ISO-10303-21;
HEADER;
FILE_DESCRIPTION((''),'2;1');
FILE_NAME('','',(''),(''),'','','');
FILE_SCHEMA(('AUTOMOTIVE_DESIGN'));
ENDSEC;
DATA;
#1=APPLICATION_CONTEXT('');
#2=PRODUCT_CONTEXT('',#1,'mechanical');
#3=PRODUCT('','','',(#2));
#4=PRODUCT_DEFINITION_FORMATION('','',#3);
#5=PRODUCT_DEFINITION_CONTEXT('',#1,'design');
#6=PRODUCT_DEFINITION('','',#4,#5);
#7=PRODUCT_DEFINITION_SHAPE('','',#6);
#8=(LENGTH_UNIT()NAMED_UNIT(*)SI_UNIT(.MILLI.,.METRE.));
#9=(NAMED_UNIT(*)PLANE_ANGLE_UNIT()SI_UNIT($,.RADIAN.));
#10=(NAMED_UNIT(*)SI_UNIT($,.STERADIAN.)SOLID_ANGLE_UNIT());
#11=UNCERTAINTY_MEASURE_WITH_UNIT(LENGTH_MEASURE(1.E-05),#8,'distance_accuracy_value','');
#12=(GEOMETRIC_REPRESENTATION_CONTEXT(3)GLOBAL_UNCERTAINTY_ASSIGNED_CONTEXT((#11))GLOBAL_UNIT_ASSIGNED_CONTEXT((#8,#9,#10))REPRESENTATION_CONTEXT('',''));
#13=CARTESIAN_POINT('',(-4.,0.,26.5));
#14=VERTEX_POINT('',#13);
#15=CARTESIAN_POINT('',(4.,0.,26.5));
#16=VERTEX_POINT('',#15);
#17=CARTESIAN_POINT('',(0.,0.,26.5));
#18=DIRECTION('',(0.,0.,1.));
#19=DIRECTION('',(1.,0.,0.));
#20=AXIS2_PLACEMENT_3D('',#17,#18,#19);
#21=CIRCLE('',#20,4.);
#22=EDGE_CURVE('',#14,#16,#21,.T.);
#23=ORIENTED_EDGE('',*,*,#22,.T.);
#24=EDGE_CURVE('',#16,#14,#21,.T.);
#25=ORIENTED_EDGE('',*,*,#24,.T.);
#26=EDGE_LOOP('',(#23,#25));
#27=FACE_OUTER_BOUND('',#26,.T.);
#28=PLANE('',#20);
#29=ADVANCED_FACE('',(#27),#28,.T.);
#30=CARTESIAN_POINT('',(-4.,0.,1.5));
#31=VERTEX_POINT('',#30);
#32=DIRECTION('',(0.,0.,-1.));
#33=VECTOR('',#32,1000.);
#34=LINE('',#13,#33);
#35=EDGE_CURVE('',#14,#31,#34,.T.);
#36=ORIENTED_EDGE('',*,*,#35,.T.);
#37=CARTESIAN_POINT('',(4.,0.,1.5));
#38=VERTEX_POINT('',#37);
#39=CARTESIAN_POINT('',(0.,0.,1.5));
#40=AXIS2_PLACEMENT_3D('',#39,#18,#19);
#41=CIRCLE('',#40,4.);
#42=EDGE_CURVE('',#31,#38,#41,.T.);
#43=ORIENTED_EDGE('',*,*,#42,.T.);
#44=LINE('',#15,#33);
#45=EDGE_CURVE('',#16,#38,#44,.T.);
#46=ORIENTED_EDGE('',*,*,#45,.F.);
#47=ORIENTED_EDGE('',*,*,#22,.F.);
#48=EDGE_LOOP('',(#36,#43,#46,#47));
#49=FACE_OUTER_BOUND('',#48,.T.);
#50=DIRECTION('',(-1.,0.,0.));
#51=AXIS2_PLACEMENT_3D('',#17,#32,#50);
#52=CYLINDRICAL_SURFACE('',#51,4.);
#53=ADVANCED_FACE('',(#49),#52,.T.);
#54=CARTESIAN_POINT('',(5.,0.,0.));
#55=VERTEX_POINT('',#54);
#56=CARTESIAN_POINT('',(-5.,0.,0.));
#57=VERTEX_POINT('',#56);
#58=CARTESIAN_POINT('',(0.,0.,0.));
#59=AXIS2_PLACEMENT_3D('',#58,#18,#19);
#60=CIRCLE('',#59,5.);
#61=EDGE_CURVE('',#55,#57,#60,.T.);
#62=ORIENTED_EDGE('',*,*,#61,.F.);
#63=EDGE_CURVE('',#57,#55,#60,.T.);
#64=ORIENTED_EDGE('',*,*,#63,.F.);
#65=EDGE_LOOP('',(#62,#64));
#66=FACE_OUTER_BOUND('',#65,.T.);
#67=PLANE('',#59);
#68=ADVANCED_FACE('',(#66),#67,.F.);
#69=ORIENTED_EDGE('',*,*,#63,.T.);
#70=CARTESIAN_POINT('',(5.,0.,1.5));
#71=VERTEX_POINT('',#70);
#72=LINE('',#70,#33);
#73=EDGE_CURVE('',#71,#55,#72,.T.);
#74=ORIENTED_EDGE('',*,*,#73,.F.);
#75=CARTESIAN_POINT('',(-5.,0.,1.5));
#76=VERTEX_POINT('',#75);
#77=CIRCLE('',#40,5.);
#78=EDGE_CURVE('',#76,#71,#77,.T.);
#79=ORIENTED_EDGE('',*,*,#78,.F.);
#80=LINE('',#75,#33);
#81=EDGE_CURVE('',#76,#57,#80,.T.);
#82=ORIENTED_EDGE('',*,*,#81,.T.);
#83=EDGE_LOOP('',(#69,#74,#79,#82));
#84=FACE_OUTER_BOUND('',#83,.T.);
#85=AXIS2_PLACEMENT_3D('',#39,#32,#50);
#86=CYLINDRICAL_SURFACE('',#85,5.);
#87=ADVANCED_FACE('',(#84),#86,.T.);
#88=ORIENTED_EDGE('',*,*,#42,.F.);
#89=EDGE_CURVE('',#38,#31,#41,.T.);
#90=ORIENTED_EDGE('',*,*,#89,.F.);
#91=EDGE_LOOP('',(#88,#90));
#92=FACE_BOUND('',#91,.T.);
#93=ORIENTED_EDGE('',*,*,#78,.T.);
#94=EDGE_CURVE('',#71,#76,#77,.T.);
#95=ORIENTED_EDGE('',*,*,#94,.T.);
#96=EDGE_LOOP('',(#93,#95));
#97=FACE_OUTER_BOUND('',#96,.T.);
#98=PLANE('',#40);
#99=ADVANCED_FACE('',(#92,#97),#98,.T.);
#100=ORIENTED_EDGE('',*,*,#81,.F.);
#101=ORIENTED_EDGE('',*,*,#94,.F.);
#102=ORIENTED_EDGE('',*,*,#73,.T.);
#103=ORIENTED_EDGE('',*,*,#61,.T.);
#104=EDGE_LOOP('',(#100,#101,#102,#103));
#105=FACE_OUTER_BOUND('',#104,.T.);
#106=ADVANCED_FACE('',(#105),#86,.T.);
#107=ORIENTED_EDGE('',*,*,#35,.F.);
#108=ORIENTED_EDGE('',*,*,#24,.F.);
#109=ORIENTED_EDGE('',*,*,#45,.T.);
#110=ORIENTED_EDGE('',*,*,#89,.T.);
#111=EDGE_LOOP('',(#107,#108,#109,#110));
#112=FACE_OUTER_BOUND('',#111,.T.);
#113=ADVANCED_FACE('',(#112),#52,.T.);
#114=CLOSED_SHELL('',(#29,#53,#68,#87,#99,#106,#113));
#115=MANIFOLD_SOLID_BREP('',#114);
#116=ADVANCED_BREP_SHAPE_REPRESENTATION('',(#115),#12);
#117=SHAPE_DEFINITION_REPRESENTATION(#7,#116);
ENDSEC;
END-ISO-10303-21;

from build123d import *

# Parameters (mm, degrees)
SKETCH_1_R      = 5
EXTRUDE_1_DEPTH = 1.5
SKETCH_2_R      = 4
EXTRUDE_2_DEPTH = 25


with BuildPart() as part:
    # 草图1 → 凸台-拉伸1 (new body)
    with BuildSketch(Plane.XY):
        Circle(SKETCH_1_R)
    extrude(amount=EXTRUDE_1_DEPTH)

    # 草图2 → 凸台-拉伸2 (add)
    with BuildSketch(Plane.XY.offset(1.5)):
        Circle(SKETCH_2_R)
    extrude(amount=EXTRUDE_2_DEPTH)


solid = part.part
